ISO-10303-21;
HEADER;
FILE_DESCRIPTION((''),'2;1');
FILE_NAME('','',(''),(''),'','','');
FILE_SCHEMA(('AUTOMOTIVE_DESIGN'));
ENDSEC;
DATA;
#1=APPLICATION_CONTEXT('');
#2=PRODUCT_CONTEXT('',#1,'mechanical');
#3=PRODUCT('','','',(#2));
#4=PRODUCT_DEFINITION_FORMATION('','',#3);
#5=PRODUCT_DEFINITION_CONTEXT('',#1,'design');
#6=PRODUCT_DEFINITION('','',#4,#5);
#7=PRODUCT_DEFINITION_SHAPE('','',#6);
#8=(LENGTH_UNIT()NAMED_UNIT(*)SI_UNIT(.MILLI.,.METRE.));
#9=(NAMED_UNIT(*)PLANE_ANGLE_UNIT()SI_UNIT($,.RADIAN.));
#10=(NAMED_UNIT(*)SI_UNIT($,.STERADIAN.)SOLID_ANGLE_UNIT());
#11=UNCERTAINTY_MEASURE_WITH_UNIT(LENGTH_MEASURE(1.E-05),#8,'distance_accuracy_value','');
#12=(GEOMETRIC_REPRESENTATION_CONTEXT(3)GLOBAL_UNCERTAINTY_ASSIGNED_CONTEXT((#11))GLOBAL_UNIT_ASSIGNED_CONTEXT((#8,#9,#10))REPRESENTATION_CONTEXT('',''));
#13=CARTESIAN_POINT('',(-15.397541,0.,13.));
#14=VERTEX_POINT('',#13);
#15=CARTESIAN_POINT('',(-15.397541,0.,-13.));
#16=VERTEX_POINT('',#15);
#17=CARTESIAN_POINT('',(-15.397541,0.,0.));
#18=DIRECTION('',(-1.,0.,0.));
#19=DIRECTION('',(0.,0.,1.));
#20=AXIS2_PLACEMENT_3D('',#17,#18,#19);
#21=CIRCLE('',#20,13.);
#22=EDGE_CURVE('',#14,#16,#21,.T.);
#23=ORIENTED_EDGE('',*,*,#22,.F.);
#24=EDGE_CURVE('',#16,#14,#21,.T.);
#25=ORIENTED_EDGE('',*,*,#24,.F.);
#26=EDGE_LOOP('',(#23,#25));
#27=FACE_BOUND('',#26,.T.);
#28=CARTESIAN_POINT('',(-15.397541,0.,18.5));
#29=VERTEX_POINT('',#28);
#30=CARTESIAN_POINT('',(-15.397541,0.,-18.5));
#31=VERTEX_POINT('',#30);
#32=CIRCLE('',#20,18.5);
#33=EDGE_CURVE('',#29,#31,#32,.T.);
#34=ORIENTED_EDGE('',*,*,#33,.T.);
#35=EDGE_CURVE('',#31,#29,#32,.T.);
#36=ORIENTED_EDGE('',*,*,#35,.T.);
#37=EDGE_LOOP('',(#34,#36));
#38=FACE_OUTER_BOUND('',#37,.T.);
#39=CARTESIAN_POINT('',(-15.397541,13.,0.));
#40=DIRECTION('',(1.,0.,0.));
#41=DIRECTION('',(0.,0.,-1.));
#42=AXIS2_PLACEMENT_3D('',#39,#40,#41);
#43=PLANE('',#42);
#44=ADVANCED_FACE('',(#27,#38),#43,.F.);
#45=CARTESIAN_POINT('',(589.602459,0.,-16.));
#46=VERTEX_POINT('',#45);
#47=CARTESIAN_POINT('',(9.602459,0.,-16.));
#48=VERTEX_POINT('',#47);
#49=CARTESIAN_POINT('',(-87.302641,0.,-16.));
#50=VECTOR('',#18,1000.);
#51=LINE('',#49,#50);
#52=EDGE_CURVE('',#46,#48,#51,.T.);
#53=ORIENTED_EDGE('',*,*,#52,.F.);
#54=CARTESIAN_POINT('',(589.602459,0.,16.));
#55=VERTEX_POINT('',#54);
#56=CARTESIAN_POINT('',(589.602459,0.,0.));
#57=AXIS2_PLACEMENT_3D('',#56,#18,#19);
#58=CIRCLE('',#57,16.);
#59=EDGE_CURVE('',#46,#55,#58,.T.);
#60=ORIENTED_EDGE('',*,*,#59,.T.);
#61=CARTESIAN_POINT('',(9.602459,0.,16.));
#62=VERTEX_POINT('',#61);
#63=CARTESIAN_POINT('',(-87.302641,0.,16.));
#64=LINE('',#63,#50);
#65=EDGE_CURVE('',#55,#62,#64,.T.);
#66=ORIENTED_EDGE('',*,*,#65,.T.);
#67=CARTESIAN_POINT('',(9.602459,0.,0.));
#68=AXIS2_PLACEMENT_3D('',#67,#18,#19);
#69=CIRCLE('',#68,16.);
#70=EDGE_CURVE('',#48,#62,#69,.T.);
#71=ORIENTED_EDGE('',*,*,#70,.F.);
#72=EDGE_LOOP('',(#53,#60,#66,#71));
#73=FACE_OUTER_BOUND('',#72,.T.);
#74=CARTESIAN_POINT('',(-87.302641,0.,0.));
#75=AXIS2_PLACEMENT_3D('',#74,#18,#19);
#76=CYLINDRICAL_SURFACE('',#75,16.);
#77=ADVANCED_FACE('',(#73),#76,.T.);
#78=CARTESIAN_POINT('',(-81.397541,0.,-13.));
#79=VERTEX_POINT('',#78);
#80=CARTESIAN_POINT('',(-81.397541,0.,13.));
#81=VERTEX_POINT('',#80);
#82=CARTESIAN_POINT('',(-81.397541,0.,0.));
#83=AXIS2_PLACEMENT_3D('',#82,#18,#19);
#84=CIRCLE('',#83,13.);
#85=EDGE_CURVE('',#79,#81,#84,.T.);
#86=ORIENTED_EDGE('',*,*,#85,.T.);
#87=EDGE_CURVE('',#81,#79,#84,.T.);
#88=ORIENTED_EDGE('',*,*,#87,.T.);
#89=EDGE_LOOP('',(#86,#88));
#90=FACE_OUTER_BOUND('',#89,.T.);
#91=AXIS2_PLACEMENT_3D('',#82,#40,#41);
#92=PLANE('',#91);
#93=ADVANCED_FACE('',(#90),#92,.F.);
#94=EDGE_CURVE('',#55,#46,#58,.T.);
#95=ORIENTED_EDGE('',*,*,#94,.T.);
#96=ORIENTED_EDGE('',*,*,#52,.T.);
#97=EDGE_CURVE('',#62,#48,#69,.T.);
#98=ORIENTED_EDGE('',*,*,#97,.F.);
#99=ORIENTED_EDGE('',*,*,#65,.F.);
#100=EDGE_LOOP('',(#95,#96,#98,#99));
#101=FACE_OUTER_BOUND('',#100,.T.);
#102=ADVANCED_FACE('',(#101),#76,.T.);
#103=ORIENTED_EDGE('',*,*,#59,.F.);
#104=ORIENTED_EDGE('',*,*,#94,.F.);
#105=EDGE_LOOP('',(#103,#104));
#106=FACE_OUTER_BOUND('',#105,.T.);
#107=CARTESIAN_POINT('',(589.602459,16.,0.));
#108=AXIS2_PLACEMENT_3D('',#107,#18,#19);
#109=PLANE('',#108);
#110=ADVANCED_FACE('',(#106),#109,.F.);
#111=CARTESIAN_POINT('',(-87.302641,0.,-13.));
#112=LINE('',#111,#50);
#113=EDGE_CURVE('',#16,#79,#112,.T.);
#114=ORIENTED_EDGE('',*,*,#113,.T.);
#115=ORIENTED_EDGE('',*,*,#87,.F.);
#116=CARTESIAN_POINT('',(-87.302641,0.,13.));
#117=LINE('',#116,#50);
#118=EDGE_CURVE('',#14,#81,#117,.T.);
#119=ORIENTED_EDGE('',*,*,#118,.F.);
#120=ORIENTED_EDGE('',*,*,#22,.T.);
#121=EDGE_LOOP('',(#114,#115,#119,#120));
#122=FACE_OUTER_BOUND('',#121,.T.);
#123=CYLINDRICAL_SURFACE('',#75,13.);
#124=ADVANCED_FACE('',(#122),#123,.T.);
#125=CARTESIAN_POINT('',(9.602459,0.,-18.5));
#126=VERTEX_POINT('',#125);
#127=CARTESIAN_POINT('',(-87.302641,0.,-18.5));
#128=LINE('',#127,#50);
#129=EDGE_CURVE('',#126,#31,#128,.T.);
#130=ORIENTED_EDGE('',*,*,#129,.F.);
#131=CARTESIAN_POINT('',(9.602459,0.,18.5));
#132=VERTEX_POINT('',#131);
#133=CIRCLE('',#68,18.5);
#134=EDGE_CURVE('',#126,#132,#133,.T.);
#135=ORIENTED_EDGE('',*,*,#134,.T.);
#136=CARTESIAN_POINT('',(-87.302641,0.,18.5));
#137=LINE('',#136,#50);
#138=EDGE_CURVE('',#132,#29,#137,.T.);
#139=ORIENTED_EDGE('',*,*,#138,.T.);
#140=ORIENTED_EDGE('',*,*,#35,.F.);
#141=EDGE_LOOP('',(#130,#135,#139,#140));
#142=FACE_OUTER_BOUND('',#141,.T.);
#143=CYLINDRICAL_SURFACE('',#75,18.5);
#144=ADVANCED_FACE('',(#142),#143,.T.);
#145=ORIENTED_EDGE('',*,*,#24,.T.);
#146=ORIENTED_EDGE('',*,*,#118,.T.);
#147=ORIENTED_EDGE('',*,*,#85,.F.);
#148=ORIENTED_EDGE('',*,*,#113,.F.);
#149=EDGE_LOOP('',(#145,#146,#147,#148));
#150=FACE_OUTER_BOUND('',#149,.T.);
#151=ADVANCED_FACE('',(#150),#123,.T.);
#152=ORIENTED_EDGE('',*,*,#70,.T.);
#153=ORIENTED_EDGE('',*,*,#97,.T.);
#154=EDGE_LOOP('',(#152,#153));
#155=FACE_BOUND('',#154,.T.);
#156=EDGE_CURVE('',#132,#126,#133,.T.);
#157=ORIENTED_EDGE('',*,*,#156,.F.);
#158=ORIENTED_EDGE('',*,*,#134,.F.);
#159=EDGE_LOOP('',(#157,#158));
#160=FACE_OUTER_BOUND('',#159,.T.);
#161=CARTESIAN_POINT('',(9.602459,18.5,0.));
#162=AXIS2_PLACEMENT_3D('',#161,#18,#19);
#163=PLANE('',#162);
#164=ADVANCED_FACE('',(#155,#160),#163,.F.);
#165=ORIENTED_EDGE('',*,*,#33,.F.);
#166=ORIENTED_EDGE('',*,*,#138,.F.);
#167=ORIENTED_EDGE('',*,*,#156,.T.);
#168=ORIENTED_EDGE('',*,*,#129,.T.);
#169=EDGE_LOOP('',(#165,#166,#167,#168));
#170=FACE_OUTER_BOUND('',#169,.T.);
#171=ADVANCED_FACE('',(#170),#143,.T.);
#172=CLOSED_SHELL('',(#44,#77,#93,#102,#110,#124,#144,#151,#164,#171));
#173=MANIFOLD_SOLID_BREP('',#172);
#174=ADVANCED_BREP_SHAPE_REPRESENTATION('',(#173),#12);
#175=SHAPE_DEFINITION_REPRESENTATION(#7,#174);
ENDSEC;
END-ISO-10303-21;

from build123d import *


with BuildPart() as part:
    # 草图1 → 旋转1 (revolve)
    with BuildSketch(Plane.XY, mode=Mode.PRIVATE) as revolve_1_sk:
        Polygon((-81.397540736, 0), (-81.397540736, 13), (-15.397540736, 13), (-15.397540736, 18.5), (9.602459264, 18.5), (9.602459264, 16), (589.602459264, 16), (589.602459264, 0), align=None)
    revolve(revolve_1_sk.sketch.rotate(Axis((-87.302640715, 0, 0), (1, 0, 0)), 90), axis=Axis((-87.302640715, 0, 0), (1, 0, 0)))


solid = part.part
